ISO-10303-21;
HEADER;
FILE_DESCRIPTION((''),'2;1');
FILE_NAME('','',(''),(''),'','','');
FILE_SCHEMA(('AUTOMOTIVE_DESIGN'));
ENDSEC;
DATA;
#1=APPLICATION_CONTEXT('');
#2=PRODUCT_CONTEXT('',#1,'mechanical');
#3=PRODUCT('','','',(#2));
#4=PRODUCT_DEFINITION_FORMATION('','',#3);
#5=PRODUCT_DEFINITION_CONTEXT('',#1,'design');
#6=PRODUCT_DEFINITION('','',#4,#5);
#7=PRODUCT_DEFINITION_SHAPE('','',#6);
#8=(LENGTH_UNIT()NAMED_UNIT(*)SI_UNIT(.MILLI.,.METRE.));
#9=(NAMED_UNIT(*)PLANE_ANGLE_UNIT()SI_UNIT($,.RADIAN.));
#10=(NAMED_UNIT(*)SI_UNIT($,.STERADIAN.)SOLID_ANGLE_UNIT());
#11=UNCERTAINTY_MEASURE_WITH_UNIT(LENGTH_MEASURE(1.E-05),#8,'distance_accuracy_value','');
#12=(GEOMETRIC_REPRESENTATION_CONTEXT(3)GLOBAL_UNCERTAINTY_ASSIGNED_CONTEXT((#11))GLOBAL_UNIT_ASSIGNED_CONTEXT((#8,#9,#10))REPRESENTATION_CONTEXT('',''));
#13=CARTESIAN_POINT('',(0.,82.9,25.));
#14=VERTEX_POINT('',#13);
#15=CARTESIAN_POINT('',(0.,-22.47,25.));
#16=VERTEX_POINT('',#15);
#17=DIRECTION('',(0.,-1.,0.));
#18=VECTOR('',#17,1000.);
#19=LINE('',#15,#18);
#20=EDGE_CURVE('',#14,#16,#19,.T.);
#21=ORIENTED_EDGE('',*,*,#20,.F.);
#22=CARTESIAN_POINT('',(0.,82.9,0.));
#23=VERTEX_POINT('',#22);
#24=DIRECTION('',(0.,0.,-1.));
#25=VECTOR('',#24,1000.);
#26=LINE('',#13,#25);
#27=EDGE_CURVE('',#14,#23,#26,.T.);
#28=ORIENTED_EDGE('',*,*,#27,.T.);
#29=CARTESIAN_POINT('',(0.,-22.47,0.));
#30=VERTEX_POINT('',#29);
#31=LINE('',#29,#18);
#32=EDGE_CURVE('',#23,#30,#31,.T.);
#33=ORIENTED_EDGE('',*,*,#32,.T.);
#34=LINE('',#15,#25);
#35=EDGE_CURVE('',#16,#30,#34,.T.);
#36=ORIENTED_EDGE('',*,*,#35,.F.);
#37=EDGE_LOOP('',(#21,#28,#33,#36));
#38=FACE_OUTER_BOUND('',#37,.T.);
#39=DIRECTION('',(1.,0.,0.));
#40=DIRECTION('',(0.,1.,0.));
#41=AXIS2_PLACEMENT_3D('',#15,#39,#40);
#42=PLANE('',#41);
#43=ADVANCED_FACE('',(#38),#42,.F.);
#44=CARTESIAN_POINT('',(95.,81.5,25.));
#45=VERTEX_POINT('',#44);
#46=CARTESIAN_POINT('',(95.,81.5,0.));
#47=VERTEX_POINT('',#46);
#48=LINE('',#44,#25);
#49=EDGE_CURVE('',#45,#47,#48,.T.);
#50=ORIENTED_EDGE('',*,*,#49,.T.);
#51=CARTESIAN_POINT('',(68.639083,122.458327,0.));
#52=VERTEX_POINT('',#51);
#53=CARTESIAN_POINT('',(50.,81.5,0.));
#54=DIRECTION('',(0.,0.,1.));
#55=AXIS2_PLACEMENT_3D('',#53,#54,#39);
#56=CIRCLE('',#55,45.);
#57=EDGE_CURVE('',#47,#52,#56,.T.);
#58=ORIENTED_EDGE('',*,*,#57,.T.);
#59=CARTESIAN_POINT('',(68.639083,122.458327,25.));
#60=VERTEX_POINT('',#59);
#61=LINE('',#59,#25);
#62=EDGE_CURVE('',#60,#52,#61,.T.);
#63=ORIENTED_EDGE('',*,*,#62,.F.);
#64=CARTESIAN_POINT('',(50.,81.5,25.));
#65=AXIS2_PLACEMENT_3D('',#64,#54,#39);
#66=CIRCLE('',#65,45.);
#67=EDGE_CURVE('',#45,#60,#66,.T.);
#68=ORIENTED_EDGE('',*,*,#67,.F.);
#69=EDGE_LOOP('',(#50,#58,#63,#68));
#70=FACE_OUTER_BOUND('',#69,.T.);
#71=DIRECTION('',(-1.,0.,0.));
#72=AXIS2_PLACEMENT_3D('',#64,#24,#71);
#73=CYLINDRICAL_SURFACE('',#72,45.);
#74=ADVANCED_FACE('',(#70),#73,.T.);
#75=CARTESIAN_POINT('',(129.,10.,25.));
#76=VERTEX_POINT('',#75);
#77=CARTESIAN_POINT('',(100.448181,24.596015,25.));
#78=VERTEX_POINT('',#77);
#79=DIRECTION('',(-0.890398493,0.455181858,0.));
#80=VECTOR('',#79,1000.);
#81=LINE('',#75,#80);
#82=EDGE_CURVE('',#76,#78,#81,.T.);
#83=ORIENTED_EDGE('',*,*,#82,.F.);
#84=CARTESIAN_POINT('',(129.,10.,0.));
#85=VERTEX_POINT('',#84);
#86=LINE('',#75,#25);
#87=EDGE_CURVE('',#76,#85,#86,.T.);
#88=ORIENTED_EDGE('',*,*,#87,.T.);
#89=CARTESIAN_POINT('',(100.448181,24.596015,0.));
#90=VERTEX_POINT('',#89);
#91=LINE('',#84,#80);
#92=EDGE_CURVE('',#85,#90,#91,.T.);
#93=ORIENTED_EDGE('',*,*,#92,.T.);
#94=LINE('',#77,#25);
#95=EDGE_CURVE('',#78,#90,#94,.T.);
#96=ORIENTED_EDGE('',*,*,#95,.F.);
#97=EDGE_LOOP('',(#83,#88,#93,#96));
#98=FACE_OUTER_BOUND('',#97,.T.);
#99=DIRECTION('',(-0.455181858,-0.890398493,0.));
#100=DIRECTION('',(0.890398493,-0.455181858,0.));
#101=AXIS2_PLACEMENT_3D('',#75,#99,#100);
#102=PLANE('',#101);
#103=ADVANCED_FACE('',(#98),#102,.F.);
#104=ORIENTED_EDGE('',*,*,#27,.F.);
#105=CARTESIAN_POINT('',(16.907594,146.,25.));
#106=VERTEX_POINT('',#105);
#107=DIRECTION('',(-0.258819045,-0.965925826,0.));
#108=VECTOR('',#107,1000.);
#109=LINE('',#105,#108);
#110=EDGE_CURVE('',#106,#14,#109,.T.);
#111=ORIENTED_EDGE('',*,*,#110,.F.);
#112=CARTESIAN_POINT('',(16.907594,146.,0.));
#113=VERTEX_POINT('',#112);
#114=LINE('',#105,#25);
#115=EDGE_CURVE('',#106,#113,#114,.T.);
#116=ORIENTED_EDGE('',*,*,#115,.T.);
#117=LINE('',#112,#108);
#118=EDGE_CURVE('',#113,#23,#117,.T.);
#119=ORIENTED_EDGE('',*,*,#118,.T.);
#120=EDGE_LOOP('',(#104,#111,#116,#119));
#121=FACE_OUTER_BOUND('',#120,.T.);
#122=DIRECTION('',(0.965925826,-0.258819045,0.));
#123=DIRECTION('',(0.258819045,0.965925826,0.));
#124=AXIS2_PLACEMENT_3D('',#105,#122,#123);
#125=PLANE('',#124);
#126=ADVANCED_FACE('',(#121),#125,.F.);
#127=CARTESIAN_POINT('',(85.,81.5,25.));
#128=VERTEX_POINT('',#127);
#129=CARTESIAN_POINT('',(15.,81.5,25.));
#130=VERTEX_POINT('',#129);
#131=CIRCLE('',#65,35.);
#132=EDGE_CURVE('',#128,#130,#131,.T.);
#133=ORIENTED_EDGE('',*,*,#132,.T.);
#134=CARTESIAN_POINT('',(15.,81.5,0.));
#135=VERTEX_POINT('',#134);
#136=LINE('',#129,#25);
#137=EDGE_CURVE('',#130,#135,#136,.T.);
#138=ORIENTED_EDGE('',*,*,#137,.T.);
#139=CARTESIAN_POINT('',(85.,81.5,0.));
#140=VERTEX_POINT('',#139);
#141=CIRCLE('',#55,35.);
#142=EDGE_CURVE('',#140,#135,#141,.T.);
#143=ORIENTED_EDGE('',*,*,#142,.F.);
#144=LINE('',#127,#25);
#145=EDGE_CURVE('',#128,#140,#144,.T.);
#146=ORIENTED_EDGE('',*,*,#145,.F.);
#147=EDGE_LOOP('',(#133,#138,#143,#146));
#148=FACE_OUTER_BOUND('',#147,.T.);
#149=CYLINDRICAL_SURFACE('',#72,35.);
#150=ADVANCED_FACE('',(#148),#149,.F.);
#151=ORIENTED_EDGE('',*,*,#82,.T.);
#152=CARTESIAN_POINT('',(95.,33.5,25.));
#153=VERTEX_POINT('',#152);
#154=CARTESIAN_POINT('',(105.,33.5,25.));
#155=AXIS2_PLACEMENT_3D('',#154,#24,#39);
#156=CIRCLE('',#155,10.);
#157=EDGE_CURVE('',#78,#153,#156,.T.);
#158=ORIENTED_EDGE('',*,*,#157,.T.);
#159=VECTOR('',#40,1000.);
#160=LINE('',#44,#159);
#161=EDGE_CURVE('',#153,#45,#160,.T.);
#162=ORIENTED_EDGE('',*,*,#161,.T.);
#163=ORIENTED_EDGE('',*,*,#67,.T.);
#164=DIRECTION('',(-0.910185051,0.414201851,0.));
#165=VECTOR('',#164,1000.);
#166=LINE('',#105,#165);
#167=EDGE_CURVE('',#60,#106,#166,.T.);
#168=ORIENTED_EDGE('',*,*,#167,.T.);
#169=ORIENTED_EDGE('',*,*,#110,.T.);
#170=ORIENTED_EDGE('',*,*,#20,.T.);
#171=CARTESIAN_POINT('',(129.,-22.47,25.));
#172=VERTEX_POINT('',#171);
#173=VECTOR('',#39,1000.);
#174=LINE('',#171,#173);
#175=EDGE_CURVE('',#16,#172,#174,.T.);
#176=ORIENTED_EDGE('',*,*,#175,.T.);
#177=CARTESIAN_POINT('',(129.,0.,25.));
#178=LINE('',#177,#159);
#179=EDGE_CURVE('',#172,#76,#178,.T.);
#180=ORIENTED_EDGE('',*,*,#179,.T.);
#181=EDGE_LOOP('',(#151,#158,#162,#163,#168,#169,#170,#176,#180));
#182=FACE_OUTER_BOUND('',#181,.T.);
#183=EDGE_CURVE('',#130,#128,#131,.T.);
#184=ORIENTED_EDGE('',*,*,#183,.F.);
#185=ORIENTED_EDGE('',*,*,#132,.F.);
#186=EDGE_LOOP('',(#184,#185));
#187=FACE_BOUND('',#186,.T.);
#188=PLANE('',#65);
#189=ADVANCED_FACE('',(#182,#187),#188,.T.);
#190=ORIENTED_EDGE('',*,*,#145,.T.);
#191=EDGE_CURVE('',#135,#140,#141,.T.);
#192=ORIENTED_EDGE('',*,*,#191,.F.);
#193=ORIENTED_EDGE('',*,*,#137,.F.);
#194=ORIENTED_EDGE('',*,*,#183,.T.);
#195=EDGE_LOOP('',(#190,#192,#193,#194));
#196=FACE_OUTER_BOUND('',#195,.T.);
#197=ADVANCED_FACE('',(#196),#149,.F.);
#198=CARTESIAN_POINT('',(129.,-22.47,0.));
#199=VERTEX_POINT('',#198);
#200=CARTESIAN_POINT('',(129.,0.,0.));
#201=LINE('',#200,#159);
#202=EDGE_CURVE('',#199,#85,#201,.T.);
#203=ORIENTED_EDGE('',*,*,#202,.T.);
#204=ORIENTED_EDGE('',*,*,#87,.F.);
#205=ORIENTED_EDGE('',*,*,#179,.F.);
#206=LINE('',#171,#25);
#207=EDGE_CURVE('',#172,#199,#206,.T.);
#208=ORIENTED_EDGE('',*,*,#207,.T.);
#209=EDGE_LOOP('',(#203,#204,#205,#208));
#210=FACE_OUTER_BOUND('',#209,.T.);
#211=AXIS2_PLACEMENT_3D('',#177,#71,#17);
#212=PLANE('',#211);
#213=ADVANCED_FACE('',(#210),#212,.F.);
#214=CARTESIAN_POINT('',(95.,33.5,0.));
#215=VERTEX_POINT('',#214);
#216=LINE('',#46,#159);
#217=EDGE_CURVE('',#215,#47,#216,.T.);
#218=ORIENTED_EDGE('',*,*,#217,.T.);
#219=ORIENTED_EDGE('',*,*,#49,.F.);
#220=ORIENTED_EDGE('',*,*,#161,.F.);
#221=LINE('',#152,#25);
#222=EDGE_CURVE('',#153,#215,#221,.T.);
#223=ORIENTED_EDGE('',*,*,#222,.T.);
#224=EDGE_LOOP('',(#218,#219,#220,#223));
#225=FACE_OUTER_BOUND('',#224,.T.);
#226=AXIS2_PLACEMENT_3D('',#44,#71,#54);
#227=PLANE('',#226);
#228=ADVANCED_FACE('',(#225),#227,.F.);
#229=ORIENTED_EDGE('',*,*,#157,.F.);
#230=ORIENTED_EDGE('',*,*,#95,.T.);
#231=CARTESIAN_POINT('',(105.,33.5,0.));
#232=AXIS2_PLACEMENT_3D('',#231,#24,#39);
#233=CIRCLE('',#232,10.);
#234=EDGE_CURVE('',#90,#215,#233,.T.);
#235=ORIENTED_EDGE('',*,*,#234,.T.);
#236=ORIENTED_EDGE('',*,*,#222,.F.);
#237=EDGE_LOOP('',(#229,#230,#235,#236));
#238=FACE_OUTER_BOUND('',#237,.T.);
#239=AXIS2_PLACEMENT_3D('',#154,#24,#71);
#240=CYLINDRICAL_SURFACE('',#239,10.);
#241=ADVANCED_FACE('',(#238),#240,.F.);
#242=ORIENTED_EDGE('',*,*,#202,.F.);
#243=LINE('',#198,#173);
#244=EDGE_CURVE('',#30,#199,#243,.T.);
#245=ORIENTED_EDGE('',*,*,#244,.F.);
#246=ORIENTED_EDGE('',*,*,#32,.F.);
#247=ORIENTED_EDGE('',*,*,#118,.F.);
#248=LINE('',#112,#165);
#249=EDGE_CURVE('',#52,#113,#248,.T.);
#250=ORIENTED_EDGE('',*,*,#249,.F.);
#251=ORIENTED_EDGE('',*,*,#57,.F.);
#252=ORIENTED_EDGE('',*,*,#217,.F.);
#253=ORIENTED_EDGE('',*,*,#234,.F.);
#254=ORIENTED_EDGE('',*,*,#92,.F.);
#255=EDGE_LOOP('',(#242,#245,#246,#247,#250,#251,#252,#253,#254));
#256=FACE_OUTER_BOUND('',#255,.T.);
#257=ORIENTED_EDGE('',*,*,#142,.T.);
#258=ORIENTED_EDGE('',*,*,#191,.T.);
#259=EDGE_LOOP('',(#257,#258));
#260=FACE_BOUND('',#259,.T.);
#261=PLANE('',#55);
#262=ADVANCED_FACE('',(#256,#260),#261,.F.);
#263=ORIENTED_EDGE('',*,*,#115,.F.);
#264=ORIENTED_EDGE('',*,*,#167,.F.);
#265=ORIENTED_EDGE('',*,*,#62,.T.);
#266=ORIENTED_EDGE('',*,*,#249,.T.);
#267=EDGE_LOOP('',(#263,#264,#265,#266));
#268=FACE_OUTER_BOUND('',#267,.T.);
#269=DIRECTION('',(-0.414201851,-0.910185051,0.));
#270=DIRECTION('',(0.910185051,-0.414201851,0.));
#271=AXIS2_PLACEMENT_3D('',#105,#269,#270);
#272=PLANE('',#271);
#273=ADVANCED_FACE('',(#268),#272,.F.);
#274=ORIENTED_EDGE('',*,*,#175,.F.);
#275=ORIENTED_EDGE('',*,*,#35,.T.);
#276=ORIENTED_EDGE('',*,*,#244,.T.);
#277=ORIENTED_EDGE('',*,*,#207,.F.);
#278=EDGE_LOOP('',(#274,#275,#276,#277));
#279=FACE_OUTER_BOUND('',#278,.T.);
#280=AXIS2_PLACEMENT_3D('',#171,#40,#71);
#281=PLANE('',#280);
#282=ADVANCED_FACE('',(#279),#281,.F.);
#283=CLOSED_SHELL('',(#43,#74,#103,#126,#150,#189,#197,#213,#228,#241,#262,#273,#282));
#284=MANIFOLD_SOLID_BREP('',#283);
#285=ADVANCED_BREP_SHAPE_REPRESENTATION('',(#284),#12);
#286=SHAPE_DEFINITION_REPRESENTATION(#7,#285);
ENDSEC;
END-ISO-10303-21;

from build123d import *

# Parameters (mm, degrees)
SKETCH_1_R      = 35
EXTRUDE_1_DEPTH = 25


with BuildPart() as part:
    # 草图1 → 凸台-拉伸1 (new body)
    with BuildSketch(Plane.XY):
        with BuildLine():
            Line((129, 0), (129, 10))
            Line((129, 10), (100.448181422, 24.59601507))
            ThreePointArc((100.448181422, 24.59601507), (96.470105928, 28.280717759), (95, 33.5))
            Line((95, 33.5), (95, 81.5))
            ThreePointArc((95, 81.5), (87.840181999, 105.854067962), (68.639083275, 122.458327293))
            Line((68.639083275, 122.458327293), (16.907594042, 146))
            Line((16.907594042, 146), (0, 82.9))
            Line((0, 82.9), (0, -22.47))
            Line((0, -22.47), (129, -22.47))
            Line((129, -22.47), (129, 0))
        make_face()
        with Locations((50, 81.5)):
            Circle(SKETCH_1_R, mode=Mode.SUBTRACT)
    extrude(amount=EXTRUDE_1_DEPTH)


solid = part.part
